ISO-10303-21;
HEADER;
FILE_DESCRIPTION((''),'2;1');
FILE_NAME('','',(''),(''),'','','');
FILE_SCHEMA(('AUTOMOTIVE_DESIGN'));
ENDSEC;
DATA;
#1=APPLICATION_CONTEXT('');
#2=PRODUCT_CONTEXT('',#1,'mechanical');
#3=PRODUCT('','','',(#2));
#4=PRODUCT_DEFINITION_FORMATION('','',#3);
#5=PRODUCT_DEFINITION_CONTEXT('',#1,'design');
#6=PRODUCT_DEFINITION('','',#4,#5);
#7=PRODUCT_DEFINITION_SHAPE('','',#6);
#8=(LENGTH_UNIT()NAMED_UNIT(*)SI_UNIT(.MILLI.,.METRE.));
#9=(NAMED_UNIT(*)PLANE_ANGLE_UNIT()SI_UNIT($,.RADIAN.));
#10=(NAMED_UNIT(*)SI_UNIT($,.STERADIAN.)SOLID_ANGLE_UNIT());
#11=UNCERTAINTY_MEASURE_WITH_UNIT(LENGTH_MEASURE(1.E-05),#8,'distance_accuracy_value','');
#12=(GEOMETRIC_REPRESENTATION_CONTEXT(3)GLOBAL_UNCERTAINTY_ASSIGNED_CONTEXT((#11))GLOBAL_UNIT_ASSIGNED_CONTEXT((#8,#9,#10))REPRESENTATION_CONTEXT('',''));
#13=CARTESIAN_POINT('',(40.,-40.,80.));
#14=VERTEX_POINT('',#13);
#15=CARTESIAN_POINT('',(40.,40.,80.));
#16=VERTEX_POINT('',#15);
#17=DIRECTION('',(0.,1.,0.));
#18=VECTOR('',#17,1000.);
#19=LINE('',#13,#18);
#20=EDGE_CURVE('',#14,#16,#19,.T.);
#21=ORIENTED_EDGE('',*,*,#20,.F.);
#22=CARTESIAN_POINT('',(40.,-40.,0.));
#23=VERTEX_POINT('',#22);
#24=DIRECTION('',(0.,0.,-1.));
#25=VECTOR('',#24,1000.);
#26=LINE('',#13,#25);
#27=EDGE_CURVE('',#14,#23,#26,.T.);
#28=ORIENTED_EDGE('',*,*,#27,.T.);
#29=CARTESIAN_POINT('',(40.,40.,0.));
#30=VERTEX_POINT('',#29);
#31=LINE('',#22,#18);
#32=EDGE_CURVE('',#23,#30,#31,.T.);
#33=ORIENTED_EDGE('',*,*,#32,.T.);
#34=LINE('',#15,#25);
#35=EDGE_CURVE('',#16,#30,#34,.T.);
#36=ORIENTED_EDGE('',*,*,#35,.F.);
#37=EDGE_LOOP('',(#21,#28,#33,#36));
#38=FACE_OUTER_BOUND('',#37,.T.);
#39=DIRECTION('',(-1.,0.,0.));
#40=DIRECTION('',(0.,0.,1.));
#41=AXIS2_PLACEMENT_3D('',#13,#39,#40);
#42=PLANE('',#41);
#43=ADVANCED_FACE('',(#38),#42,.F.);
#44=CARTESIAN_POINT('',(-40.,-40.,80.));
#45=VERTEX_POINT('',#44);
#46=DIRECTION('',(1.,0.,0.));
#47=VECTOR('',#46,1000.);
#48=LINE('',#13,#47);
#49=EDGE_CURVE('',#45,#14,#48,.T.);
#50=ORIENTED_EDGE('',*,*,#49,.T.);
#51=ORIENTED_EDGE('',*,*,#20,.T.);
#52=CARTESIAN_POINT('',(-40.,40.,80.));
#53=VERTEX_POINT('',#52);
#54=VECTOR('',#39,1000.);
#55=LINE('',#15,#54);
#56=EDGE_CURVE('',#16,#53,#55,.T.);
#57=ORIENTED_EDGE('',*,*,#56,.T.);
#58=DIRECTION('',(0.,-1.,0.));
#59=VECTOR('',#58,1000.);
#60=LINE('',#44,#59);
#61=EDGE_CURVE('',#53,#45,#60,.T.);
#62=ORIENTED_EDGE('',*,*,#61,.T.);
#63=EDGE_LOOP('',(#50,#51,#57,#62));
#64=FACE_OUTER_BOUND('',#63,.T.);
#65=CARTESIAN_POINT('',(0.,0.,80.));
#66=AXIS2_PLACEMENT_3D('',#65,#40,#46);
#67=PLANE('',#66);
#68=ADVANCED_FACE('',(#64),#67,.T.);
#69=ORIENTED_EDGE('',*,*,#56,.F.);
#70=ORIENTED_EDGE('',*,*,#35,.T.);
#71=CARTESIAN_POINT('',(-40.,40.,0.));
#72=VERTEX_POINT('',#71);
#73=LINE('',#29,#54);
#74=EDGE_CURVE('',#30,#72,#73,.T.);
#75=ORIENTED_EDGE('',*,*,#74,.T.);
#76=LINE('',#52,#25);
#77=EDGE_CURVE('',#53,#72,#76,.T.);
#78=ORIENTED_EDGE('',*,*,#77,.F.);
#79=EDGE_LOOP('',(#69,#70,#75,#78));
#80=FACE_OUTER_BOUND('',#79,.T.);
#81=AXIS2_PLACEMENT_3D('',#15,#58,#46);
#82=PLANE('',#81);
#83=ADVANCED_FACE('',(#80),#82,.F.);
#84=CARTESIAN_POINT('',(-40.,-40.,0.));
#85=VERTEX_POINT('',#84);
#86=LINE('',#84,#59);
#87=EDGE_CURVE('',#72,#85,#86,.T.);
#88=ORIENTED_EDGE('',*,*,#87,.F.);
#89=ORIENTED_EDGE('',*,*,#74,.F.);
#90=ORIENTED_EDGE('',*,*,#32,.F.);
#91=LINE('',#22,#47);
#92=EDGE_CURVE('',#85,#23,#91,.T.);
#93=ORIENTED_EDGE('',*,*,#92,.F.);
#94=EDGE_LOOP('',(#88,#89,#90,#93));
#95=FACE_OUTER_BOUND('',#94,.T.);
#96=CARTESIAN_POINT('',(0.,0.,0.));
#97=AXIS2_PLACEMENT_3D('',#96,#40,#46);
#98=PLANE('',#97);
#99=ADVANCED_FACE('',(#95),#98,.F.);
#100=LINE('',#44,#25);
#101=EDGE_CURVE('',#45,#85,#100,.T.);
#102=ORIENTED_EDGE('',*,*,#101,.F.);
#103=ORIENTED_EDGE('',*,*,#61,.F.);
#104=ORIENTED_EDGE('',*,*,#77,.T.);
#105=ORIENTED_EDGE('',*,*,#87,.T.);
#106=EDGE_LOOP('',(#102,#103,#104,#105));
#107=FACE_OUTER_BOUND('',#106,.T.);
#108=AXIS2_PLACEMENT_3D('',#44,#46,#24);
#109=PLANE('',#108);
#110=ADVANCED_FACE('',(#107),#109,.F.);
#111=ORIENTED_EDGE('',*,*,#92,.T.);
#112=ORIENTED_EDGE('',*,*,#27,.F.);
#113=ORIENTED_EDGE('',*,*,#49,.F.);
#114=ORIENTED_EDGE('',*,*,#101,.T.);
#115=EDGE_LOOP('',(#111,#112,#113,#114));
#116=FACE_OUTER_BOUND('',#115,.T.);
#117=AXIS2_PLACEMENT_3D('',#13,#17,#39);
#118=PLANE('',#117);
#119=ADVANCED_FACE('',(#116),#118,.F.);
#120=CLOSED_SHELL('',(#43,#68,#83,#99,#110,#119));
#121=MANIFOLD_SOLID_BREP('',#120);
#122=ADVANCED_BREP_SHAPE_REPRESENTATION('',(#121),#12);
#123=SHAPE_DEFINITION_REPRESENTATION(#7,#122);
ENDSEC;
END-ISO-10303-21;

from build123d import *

# Parameters (mm, degrees)
SKETCH_1_W      = 80
SKETCH_1_H      = 80
EXTRUDE_1_DEPTH = 80


with BuildPart() as part:
    # 草图1 → 凸台-拉伸1 (new body)
    with BuildSketch(Plane.XY):
        Rectangle(SKETCH_1_W, SKETCH_1_H)
    extrude(amount=EXTRUDE_1_DEPTH)


solid = part.part
